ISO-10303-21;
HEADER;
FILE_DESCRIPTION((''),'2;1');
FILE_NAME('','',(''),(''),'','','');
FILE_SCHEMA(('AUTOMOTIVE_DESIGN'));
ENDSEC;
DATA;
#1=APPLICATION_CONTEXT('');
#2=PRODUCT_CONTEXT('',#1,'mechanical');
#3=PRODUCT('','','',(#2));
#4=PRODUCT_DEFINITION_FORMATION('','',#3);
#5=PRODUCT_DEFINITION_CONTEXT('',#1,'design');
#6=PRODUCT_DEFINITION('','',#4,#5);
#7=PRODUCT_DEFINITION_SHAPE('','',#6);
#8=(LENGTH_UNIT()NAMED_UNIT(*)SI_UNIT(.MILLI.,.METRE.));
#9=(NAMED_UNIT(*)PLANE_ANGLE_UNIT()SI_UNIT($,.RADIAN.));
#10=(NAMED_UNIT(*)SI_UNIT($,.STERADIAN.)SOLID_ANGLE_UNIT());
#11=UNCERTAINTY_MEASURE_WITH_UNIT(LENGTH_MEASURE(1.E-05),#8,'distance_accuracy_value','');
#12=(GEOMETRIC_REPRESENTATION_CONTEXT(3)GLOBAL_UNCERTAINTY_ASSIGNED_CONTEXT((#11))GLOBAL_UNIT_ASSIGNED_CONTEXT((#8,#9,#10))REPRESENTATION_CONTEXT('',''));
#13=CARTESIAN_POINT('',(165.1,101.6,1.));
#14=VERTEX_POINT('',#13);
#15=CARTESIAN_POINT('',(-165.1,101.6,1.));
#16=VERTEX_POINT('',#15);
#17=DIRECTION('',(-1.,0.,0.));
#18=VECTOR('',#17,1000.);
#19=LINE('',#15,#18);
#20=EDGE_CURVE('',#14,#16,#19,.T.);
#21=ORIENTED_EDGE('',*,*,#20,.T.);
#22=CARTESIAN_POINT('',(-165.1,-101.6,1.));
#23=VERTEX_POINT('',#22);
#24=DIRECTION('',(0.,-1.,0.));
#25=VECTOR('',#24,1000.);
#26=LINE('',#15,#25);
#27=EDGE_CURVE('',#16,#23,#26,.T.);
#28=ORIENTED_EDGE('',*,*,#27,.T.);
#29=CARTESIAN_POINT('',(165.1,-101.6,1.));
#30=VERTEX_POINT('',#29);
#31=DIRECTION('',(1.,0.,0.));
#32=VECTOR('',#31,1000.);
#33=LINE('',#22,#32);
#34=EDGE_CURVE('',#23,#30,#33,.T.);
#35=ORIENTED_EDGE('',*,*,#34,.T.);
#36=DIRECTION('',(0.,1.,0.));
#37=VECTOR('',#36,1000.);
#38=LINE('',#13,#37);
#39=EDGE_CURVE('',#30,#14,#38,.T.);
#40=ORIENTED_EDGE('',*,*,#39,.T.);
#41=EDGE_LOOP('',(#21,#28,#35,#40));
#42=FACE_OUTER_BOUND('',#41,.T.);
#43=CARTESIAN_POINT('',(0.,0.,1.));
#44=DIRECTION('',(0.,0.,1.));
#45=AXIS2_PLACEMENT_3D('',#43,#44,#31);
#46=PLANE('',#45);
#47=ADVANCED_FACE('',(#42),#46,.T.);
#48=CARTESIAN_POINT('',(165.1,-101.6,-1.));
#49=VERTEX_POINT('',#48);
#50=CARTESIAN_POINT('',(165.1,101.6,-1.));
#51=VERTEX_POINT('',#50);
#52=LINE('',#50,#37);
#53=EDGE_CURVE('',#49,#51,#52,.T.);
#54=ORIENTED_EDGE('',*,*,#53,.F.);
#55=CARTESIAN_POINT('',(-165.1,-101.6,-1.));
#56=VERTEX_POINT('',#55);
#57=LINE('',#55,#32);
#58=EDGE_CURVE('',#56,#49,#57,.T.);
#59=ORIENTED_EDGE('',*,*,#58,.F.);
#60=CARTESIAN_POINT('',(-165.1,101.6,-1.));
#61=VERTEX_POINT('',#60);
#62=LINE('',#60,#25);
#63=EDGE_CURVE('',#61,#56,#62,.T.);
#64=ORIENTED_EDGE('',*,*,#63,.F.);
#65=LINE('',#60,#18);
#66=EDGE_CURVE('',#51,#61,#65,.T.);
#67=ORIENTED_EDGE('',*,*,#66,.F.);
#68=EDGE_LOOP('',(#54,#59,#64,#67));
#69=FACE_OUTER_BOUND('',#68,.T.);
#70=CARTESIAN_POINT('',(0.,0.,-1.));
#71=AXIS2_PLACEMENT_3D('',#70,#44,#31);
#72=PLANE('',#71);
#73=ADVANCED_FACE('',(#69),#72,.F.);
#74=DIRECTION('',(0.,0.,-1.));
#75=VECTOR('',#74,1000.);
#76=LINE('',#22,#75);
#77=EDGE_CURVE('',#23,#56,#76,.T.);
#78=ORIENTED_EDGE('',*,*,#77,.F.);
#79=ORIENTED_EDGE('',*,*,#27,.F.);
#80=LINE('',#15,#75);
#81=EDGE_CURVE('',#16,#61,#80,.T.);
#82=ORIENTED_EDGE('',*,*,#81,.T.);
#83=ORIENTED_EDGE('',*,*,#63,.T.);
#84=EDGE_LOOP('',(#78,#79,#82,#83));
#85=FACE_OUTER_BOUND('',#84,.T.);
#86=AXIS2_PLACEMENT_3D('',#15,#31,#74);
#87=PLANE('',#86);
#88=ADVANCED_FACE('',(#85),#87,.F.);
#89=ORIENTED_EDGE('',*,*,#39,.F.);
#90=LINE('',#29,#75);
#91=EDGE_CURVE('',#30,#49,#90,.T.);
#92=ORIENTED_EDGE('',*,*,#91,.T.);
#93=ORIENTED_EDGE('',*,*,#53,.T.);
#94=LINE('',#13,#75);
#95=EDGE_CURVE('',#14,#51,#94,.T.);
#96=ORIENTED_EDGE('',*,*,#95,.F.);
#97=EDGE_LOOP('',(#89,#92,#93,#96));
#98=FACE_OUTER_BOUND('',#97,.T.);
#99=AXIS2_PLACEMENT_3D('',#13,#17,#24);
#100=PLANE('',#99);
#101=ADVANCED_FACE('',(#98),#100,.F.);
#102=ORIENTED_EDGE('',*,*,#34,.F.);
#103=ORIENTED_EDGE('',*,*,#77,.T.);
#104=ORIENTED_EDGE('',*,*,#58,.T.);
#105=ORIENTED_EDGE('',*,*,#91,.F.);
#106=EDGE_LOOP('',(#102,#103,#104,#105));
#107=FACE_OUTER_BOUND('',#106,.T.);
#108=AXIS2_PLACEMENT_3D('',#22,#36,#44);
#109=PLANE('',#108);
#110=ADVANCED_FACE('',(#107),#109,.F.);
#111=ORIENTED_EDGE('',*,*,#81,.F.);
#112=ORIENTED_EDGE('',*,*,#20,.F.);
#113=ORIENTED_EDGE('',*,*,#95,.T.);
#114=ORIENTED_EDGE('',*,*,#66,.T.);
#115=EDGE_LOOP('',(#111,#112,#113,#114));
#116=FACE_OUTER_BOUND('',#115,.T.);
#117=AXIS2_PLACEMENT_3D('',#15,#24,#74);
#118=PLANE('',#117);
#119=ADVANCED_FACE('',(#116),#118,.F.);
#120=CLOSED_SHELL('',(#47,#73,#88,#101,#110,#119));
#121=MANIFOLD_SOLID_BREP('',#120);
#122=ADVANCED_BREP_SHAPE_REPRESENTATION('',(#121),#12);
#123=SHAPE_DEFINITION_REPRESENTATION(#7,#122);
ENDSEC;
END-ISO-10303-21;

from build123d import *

# Parameters (mm, degrees)
SKETCH1_W           = 330.2
SKETCH1_H           = 203.2
BOSS_EXTRUDE1_DEPTH = 1


with BuildPart() as part:
    # Sketch1 → Boss-Extrude1 (new, symmetric)
    with BuildSketch(Plane.XY):
        Rectangle(SKETCH1_W, SKETCH1_H)
    extrude(amount=BOSS_EXTRUDE1_DEPTH, both=True)


solid = part.part
